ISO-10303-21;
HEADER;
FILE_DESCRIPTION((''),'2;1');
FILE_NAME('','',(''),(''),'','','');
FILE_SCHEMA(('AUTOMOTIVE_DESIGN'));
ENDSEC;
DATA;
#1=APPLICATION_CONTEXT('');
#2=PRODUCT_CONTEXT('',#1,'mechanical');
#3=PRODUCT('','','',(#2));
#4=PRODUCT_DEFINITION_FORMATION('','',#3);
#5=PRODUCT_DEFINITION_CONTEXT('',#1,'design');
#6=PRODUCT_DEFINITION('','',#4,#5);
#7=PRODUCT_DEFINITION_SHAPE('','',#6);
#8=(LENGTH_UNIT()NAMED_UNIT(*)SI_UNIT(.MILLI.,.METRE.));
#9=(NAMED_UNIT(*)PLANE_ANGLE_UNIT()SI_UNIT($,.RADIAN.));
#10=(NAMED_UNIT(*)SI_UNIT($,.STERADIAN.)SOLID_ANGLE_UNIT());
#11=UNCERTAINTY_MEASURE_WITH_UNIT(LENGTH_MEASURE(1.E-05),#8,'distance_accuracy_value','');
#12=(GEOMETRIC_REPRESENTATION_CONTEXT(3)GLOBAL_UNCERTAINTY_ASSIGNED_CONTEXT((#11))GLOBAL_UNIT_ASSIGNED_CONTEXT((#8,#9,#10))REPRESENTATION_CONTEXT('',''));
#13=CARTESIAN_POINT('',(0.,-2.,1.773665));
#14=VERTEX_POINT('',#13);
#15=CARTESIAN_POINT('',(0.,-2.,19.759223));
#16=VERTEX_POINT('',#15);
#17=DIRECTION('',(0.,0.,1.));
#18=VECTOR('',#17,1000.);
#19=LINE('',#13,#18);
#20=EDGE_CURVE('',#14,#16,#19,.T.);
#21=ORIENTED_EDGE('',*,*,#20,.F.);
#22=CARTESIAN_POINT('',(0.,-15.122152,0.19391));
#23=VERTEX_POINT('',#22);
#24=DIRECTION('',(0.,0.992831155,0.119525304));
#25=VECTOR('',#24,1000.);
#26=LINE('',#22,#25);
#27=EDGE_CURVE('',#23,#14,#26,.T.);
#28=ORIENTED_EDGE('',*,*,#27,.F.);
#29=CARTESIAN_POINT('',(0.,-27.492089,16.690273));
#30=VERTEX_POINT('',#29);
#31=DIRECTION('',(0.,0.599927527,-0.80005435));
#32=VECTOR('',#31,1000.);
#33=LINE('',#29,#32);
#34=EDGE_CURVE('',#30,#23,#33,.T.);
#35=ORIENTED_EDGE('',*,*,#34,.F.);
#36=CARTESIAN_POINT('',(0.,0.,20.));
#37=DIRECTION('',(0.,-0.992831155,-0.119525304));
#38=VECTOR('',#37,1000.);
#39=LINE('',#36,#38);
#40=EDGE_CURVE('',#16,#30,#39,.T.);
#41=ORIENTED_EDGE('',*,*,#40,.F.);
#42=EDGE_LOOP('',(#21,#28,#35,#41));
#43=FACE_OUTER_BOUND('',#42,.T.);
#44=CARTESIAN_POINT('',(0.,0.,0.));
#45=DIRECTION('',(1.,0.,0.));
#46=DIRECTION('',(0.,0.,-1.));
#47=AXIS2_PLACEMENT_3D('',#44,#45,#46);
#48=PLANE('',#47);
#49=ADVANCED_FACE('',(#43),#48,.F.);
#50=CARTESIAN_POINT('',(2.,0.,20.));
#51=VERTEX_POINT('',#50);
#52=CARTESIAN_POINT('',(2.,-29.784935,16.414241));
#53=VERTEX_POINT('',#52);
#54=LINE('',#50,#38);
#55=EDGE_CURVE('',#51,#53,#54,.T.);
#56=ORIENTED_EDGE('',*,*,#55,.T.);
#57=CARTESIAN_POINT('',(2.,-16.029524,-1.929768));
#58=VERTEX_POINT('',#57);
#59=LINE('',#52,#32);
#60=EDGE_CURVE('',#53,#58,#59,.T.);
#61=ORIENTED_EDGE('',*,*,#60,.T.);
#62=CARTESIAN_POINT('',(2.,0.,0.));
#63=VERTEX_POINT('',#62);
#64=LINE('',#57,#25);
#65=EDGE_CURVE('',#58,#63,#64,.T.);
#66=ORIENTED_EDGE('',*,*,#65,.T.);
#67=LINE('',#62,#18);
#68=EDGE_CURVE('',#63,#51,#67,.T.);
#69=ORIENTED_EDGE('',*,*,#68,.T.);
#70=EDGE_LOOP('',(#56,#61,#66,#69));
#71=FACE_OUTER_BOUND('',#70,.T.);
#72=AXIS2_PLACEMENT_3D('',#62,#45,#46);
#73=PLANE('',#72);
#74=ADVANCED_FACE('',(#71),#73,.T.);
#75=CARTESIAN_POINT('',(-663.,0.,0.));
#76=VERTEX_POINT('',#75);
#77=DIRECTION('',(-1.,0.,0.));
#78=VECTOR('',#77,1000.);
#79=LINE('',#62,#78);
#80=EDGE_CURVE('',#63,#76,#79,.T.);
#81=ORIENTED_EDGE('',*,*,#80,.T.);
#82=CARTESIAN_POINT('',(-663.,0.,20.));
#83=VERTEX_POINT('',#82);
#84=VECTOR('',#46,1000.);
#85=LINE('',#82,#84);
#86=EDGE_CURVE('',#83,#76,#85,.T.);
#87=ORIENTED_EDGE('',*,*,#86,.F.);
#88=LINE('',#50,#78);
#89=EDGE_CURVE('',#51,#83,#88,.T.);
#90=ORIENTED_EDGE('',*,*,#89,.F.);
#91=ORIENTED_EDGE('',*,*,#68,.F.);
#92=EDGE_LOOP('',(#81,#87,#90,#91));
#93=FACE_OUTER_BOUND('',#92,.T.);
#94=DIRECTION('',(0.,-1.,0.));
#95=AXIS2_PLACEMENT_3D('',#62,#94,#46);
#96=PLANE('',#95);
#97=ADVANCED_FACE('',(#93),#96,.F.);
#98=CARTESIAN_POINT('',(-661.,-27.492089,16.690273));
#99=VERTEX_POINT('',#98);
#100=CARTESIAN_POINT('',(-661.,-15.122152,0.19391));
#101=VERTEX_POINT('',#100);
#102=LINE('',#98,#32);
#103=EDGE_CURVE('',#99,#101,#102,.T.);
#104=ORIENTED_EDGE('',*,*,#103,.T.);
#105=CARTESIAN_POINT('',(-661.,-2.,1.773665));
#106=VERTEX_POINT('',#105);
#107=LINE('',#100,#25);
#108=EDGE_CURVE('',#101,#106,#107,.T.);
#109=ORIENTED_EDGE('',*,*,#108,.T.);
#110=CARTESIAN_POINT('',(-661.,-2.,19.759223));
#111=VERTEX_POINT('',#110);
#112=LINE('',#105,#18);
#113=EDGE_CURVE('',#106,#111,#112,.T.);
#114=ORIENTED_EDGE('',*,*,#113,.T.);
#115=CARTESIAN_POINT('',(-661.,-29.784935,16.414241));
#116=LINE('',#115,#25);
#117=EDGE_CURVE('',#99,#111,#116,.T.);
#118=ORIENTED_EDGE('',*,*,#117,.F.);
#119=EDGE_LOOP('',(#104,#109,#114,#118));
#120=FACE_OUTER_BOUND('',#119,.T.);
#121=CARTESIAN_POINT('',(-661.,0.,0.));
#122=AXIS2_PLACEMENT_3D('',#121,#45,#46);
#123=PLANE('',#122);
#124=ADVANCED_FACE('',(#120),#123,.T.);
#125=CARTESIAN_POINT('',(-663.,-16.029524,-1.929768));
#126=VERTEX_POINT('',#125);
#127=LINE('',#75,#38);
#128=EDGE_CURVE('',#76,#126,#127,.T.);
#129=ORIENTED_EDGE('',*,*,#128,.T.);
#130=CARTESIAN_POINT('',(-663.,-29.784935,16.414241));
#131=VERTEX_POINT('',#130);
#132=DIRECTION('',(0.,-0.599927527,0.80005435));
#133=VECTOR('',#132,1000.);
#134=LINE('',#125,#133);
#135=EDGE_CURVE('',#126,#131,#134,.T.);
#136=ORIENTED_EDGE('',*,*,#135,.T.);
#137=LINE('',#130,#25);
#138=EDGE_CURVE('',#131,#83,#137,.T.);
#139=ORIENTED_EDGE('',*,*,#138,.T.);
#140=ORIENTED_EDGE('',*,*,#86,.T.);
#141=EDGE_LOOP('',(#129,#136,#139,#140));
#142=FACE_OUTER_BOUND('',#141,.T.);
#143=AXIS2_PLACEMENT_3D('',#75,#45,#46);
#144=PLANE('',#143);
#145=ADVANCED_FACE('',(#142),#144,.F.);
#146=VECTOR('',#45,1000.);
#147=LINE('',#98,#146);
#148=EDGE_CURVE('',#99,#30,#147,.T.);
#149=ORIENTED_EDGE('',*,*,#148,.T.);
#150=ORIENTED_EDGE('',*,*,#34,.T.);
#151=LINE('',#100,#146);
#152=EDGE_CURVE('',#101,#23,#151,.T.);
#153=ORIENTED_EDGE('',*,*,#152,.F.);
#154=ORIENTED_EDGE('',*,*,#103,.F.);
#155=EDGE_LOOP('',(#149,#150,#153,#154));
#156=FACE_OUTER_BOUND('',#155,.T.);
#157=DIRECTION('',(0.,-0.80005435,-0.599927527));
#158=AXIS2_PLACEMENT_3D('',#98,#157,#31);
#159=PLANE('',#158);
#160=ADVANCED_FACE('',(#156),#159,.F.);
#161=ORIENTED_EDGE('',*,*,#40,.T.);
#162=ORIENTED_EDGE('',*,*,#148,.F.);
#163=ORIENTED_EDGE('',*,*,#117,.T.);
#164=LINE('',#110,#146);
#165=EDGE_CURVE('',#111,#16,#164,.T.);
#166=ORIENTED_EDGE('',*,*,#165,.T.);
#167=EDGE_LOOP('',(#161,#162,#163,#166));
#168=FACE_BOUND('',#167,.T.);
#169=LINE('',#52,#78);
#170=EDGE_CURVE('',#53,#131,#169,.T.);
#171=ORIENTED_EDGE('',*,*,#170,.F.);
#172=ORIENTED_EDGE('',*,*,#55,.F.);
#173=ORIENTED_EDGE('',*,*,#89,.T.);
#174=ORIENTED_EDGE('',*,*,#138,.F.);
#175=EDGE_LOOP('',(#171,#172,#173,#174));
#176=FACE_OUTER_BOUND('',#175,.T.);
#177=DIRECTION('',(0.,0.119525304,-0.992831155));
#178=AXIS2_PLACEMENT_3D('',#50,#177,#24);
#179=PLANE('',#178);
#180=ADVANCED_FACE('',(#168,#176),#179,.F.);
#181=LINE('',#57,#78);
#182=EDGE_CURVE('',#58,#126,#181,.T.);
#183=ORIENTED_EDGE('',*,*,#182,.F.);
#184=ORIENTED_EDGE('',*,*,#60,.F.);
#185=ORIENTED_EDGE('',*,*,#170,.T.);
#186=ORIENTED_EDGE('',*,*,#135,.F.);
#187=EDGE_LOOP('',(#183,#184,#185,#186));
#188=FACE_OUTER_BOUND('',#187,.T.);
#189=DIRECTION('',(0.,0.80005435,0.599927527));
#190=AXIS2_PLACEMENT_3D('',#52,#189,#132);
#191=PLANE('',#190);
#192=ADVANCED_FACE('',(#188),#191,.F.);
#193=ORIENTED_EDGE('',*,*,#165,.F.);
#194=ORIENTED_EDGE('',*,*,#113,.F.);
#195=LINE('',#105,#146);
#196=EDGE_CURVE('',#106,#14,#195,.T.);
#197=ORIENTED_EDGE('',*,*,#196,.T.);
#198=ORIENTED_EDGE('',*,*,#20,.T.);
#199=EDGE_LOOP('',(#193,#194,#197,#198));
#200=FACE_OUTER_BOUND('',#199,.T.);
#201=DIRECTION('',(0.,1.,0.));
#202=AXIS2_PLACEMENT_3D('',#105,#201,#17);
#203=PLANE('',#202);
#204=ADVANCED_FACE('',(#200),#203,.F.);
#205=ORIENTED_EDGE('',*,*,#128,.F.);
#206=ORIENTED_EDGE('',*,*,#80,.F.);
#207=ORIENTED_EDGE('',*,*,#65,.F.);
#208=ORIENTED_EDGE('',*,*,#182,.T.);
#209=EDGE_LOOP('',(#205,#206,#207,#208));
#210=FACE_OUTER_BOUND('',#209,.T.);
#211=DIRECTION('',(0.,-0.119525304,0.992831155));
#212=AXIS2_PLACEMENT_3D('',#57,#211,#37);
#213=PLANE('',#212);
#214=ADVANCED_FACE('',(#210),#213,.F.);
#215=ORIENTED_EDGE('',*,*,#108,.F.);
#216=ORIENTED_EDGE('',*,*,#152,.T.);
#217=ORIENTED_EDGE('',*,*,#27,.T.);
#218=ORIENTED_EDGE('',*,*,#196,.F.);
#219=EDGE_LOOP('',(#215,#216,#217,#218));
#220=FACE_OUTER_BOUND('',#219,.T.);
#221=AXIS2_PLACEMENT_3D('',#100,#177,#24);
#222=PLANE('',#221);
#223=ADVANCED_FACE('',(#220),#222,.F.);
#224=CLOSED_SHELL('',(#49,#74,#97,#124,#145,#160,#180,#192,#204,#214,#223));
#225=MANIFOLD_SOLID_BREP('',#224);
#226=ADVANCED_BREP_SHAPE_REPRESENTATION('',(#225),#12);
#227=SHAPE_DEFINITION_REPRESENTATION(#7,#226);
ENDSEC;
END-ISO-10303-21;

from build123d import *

# Parameters (mm, degrees)
BOSS_EXTRUDE1_DEPTH = 2
BOSS_EXTRUDE2_DEPTH = 661
BOSS_EXTRUDE3_DEPTH = 2


with BuildPart() as part:
    # Sketch1 → Boss-Extrude1 (new body)
    with BuildSketch(Plane(origin=(0, 0, 0), x_dir=(0, 0, -1), z_dir=(1, 0, 0))):
        Polygon((0, 0), (-20, 0), (-16.414240878, -29.78493464), (1.929767975, -16.029524307), align=None)
    extrude(amount=BOSS_EXTRUDE1_DEPTH)

    # Sketch2 → Boss-Extrude2 (add)
    with BuildSketch(Plane.ZY):
        Polygon((0, 0), (20, 0), (19.759223301, -2), (1.773664518, -2), (0.193910267, -15.122152246), (16.690272744, -27.492089303), (16.414240878, -29.78493464), (-1.929767975, -16.029524307), align=None)
    extrude(amount=BOSS_EXTRUDE2_DEPTH)

    # Sketch3 → Boss-Extrude3 (add)
    with BuildSketch(Plane.ZY.offset(661)):
        Polygon((20, 0), (0, 0), (-1.929767975, -16.029524307), (16.414240878, -29.78493464), align=None)
    extrude(amount=BOSS_EXTRUDE3_DEPTH)


solid = part.part
